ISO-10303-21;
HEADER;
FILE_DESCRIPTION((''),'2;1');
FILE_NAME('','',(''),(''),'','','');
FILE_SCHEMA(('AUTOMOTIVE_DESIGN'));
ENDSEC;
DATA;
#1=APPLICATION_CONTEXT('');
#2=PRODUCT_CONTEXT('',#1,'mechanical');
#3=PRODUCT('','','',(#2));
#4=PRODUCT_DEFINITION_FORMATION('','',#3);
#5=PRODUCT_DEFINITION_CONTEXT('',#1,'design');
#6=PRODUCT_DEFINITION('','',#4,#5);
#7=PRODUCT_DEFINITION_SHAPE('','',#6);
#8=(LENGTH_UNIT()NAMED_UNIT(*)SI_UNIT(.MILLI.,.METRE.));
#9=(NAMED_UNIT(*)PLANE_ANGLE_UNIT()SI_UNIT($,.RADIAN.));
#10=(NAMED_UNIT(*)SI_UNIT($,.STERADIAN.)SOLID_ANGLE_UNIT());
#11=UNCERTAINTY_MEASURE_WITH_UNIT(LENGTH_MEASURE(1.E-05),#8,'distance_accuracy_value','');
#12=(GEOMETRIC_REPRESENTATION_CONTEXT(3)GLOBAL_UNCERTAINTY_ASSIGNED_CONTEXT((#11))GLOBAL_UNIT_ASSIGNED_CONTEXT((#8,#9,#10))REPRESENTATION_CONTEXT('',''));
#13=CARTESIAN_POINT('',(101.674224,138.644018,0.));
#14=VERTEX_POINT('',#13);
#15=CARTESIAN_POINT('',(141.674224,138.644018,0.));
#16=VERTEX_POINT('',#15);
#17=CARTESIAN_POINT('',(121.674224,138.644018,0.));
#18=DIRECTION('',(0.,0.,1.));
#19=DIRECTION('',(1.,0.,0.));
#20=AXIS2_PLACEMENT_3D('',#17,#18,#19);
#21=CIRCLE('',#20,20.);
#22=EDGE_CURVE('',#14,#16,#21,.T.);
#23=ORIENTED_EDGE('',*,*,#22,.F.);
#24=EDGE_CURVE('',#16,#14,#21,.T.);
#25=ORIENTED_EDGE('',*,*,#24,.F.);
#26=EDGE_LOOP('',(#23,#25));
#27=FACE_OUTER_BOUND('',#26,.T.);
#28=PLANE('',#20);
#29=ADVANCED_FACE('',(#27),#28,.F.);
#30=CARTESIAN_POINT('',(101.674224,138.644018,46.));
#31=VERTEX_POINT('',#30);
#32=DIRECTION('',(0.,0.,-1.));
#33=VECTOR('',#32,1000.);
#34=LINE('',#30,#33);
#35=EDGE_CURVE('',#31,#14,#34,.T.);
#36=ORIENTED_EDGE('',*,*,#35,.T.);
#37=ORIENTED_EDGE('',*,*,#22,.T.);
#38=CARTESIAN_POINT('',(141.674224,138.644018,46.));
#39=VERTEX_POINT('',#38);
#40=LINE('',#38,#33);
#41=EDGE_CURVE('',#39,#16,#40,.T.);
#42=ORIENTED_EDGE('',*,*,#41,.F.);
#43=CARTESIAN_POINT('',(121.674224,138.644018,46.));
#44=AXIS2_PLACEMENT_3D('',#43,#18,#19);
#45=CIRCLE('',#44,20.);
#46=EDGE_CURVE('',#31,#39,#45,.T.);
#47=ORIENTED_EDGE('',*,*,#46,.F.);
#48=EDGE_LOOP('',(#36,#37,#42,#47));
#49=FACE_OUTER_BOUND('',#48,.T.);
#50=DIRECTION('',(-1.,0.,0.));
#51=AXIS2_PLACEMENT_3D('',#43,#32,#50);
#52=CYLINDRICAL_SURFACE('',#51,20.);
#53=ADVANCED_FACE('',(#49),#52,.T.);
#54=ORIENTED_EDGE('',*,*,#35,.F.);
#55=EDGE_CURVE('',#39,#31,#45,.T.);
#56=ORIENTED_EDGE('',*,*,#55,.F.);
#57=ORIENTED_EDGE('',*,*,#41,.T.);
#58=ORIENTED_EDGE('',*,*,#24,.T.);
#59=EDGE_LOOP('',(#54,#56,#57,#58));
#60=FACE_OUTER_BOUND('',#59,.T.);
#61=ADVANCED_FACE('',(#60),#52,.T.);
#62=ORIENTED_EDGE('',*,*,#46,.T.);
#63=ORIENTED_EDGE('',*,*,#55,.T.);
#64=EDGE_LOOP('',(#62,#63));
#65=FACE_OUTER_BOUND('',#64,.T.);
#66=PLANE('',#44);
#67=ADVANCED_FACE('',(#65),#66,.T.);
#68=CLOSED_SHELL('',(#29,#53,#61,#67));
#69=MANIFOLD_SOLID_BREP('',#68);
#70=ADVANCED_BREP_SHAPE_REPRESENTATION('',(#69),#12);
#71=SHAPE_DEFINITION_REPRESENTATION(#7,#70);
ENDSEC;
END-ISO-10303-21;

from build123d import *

# Parameters (mm, degrees)
SKETCH2_R           = 20
BOSS_EXTRUDE1_DEPTH = 46


with BuildPart() as part:
    # Sketch2 → Boss-Extrude1 (new body)
    with BuildSketch(Plane.XY):
        with Locations((121.674224319, 138.644018399)):
            Circle(SKETCH2_R)
    extrude(amount=BOSS_EXTRUDE1_DEPTH)


solid = part.part
